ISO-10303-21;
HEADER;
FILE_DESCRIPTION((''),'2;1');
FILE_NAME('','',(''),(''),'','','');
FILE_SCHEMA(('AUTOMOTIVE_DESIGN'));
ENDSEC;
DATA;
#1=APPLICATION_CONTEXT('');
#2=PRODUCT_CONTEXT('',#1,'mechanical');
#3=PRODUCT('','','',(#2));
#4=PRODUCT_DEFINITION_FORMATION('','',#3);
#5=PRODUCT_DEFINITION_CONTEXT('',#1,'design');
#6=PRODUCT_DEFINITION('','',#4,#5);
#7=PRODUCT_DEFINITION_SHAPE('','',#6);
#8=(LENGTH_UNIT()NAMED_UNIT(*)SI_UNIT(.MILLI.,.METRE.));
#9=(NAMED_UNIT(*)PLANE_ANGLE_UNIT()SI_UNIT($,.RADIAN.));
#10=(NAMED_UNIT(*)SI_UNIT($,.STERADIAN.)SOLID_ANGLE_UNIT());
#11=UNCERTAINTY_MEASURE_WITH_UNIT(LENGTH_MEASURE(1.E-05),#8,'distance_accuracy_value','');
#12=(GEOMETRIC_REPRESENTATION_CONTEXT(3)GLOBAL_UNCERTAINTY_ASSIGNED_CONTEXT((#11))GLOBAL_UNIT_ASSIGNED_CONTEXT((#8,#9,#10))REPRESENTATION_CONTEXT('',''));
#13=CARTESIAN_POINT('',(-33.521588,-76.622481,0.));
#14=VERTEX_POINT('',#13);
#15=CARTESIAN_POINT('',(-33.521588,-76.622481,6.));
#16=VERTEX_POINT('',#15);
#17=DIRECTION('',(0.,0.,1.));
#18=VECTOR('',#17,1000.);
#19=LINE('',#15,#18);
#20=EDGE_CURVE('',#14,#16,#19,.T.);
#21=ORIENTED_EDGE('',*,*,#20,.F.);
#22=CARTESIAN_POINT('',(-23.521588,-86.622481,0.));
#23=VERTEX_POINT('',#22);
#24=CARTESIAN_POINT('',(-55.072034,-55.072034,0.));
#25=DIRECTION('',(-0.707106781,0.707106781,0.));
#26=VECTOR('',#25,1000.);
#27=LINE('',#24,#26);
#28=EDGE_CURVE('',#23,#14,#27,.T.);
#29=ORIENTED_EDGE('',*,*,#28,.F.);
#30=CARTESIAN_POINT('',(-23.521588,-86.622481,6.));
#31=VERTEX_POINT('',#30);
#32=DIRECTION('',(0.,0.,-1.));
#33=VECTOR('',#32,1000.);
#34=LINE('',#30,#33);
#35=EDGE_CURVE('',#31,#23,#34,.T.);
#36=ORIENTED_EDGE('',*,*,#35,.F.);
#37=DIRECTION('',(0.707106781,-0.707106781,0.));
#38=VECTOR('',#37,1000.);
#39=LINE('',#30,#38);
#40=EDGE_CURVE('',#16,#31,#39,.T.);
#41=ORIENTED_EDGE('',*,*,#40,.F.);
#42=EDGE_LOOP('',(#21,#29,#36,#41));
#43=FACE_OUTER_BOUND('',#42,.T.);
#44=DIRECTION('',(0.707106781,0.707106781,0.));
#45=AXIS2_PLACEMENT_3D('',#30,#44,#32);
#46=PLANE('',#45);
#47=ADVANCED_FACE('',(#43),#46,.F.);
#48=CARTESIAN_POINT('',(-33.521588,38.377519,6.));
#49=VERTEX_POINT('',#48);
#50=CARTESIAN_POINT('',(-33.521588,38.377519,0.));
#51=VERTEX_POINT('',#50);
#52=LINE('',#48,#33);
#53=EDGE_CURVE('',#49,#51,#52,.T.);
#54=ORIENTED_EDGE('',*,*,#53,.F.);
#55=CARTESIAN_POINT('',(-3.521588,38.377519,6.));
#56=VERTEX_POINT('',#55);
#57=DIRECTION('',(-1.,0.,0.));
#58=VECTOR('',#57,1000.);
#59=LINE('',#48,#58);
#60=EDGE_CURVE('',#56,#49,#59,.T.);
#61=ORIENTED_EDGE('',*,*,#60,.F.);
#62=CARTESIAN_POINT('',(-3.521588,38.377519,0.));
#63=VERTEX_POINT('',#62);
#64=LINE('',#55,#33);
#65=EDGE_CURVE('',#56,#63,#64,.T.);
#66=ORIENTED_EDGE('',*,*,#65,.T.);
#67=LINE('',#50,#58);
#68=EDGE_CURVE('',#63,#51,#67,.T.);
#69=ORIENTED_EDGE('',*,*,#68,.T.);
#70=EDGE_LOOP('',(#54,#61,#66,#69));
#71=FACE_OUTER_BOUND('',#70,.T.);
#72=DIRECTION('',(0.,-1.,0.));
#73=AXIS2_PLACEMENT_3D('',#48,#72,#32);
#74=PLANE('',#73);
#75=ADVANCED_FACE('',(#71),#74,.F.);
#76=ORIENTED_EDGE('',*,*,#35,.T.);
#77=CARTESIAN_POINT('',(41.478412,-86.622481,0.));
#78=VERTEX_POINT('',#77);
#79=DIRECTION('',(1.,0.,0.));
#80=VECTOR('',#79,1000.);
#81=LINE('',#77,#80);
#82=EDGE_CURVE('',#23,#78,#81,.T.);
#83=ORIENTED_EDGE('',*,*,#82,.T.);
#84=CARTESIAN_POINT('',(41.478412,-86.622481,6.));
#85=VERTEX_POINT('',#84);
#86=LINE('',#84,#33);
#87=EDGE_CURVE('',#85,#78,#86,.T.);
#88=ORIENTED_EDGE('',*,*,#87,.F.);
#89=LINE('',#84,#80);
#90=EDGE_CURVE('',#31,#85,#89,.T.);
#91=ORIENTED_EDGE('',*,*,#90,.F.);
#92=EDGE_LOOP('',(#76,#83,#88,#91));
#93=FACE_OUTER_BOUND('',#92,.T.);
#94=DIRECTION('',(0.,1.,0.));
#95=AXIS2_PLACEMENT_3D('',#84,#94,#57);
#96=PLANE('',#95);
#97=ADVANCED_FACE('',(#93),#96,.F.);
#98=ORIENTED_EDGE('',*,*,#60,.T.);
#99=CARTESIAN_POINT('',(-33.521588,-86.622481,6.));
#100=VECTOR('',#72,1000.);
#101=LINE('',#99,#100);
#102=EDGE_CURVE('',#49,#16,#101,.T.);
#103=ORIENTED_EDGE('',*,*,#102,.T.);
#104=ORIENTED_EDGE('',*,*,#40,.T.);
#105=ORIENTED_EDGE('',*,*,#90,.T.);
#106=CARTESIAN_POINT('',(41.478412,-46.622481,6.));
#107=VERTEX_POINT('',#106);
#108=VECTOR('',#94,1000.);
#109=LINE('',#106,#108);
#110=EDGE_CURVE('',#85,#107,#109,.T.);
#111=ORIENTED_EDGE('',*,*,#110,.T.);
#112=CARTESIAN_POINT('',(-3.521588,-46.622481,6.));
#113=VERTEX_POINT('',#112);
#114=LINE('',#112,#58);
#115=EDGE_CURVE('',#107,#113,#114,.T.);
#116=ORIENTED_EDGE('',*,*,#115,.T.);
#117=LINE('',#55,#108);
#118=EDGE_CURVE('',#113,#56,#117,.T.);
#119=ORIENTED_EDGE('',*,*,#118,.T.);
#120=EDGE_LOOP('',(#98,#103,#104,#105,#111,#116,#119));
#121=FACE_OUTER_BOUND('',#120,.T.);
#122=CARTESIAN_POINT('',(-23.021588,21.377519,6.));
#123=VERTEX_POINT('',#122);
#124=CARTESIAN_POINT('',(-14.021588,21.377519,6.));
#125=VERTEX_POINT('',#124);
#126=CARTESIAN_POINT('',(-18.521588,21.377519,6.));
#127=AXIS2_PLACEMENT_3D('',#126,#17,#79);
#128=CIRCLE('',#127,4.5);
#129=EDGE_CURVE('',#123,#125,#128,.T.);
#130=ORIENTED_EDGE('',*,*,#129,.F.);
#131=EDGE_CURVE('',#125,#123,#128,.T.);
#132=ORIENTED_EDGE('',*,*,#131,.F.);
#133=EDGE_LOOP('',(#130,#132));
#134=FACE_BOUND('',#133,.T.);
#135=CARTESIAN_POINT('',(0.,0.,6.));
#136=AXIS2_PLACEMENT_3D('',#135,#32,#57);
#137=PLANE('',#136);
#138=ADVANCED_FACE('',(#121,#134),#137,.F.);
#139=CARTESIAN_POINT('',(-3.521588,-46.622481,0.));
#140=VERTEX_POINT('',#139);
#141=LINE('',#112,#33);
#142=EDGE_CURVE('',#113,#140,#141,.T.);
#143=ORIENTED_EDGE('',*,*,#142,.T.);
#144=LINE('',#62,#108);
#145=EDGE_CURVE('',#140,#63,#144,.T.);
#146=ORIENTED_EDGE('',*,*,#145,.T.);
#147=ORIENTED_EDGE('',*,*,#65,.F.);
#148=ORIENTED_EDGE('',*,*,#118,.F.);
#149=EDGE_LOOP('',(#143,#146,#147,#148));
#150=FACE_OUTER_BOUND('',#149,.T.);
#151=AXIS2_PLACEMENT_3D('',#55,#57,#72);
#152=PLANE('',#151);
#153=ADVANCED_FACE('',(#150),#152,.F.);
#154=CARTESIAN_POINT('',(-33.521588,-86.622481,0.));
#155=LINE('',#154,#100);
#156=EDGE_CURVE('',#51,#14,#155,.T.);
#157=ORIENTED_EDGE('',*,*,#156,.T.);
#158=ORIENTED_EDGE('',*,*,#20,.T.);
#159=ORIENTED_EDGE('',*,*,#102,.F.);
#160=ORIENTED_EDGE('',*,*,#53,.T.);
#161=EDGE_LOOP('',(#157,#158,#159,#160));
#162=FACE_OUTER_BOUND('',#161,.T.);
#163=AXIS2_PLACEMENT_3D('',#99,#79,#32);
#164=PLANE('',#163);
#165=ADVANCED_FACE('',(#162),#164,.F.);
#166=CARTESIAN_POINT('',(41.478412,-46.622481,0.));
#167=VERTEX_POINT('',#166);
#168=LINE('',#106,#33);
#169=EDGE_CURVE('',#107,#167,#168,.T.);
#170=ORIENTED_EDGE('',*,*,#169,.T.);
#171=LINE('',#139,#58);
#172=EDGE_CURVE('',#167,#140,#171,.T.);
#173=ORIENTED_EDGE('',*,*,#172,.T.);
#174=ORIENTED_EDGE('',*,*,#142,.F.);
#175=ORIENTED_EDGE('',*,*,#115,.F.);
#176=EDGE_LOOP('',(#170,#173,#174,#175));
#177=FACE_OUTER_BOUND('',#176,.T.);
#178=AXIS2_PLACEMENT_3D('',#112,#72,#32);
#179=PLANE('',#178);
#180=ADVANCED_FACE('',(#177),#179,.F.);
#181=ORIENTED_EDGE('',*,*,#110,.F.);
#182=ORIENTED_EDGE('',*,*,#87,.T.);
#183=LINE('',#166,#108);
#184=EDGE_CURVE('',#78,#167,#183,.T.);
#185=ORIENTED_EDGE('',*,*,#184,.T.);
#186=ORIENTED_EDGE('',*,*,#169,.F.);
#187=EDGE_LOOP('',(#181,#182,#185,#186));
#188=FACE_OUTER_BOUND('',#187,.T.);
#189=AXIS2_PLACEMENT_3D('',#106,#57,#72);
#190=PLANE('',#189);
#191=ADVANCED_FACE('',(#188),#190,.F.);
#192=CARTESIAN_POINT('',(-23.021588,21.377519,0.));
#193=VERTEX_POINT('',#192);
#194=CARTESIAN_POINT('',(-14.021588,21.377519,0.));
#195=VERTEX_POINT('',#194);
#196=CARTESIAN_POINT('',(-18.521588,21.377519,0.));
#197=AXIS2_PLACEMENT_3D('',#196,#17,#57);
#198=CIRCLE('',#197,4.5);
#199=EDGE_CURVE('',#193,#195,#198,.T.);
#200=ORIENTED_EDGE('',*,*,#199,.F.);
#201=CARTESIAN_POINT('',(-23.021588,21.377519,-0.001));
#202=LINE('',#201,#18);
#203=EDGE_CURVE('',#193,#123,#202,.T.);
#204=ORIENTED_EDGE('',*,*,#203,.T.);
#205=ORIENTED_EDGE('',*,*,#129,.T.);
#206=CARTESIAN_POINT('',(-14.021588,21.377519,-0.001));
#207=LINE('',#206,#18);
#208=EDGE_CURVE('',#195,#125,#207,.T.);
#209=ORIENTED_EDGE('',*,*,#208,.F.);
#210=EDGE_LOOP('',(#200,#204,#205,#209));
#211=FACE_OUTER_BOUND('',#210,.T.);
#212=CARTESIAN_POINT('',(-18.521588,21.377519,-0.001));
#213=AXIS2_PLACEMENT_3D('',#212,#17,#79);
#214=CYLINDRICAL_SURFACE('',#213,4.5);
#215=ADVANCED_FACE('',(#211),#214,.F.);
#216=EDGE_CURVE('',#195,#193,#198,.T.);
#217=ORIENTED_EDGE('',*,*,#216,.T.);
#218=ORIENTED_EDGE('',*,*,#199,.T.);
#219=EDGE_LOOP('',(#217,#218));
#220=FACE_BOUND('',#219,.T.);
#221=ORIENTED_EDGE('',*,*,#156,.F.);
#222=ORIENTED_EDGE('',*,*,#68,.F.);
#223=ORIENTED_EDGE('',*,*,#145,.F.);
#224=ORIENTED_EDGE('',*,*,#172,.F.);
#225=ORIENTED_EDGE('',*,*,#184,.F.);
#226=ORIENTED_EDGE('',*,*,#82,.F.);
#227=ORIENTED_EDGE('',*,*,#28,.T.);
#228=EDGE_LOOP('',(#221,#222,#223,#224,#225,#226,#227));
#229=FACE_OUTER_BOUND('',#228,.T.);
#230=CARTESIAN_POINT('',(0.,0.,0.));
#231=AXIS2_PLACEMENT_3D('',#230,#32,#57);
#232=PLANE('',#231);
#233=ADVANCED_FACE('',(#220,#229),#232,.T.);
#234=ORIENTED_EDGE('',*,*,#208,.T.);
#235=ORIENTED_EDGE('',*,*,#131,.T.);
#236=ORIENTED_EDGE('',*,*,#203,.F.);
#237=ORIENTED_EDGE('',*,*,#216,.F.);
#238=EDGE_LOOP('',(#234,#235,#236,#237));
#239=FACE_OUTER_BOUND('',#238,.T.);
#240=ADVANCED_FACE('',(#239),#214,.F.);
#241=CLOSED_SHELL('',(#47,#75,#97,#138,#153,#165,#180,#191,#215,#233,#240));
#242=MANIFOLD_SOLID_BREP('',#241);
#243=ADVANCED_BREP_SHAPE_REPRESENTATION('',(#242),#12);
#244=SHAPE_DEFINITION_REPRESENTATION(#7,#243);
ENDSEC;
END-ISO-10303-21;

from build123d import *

# Parameters (mm, degrees)
BOSS_EXTRUDE1_DEPTH = 6
CUT_EXTRUDE1_REACH  = 98.228
SKETCH2_R           = 4.5
CHAMFER1_SIZE       = 10


with BuildPart() as part:
    # Sketch1 → Boss-Extrude1 (new body)
    with BuildSketch(Plane.XY):
        Polygon((-33.521587555, -86.6224812), (-33.521587555, 38.3775188), (-3.521587555, 38.3775188), (-3.521587555, -46.6224812), (41.478412445, -46.6224812), (41.478412445, -86.6224812), align=None)
    extrude(amount=BOSS_EXTRUDE1_DEPTH)

    # Sketch2 → Cut-Extrude1 (cut, up to next)
    with BuildSketch(Plane.XY.offset(6), mode=Mode.PRIVATE) as cut_extrude1_sk1:
        with Locations((-18.521587555, 21.3775188)):
            Circle(SKETCH2_R)
    cut_extrude1_tool1 = extrude(cut_extrude1_sk1.sketch, amount=-CUT_EXTRUDE1_REACH, mode=Mode.PRIVATE) & part.part
    add(cut_extrude1_tool1.solids().sort_by_distance((-18.521588, 21.377519, 6))[0], mode=Mode.SUBTRACT)

    # Chamfer1
    chamfer1_edges = [part.edges().sort_by_distance(p)[0] for p in [
        (-33.521587555, -86.6224812, 3),
    ]]
    chamfer(chamfer1_edges, length=CHAMFER1_SIZE)


solid = part.part
